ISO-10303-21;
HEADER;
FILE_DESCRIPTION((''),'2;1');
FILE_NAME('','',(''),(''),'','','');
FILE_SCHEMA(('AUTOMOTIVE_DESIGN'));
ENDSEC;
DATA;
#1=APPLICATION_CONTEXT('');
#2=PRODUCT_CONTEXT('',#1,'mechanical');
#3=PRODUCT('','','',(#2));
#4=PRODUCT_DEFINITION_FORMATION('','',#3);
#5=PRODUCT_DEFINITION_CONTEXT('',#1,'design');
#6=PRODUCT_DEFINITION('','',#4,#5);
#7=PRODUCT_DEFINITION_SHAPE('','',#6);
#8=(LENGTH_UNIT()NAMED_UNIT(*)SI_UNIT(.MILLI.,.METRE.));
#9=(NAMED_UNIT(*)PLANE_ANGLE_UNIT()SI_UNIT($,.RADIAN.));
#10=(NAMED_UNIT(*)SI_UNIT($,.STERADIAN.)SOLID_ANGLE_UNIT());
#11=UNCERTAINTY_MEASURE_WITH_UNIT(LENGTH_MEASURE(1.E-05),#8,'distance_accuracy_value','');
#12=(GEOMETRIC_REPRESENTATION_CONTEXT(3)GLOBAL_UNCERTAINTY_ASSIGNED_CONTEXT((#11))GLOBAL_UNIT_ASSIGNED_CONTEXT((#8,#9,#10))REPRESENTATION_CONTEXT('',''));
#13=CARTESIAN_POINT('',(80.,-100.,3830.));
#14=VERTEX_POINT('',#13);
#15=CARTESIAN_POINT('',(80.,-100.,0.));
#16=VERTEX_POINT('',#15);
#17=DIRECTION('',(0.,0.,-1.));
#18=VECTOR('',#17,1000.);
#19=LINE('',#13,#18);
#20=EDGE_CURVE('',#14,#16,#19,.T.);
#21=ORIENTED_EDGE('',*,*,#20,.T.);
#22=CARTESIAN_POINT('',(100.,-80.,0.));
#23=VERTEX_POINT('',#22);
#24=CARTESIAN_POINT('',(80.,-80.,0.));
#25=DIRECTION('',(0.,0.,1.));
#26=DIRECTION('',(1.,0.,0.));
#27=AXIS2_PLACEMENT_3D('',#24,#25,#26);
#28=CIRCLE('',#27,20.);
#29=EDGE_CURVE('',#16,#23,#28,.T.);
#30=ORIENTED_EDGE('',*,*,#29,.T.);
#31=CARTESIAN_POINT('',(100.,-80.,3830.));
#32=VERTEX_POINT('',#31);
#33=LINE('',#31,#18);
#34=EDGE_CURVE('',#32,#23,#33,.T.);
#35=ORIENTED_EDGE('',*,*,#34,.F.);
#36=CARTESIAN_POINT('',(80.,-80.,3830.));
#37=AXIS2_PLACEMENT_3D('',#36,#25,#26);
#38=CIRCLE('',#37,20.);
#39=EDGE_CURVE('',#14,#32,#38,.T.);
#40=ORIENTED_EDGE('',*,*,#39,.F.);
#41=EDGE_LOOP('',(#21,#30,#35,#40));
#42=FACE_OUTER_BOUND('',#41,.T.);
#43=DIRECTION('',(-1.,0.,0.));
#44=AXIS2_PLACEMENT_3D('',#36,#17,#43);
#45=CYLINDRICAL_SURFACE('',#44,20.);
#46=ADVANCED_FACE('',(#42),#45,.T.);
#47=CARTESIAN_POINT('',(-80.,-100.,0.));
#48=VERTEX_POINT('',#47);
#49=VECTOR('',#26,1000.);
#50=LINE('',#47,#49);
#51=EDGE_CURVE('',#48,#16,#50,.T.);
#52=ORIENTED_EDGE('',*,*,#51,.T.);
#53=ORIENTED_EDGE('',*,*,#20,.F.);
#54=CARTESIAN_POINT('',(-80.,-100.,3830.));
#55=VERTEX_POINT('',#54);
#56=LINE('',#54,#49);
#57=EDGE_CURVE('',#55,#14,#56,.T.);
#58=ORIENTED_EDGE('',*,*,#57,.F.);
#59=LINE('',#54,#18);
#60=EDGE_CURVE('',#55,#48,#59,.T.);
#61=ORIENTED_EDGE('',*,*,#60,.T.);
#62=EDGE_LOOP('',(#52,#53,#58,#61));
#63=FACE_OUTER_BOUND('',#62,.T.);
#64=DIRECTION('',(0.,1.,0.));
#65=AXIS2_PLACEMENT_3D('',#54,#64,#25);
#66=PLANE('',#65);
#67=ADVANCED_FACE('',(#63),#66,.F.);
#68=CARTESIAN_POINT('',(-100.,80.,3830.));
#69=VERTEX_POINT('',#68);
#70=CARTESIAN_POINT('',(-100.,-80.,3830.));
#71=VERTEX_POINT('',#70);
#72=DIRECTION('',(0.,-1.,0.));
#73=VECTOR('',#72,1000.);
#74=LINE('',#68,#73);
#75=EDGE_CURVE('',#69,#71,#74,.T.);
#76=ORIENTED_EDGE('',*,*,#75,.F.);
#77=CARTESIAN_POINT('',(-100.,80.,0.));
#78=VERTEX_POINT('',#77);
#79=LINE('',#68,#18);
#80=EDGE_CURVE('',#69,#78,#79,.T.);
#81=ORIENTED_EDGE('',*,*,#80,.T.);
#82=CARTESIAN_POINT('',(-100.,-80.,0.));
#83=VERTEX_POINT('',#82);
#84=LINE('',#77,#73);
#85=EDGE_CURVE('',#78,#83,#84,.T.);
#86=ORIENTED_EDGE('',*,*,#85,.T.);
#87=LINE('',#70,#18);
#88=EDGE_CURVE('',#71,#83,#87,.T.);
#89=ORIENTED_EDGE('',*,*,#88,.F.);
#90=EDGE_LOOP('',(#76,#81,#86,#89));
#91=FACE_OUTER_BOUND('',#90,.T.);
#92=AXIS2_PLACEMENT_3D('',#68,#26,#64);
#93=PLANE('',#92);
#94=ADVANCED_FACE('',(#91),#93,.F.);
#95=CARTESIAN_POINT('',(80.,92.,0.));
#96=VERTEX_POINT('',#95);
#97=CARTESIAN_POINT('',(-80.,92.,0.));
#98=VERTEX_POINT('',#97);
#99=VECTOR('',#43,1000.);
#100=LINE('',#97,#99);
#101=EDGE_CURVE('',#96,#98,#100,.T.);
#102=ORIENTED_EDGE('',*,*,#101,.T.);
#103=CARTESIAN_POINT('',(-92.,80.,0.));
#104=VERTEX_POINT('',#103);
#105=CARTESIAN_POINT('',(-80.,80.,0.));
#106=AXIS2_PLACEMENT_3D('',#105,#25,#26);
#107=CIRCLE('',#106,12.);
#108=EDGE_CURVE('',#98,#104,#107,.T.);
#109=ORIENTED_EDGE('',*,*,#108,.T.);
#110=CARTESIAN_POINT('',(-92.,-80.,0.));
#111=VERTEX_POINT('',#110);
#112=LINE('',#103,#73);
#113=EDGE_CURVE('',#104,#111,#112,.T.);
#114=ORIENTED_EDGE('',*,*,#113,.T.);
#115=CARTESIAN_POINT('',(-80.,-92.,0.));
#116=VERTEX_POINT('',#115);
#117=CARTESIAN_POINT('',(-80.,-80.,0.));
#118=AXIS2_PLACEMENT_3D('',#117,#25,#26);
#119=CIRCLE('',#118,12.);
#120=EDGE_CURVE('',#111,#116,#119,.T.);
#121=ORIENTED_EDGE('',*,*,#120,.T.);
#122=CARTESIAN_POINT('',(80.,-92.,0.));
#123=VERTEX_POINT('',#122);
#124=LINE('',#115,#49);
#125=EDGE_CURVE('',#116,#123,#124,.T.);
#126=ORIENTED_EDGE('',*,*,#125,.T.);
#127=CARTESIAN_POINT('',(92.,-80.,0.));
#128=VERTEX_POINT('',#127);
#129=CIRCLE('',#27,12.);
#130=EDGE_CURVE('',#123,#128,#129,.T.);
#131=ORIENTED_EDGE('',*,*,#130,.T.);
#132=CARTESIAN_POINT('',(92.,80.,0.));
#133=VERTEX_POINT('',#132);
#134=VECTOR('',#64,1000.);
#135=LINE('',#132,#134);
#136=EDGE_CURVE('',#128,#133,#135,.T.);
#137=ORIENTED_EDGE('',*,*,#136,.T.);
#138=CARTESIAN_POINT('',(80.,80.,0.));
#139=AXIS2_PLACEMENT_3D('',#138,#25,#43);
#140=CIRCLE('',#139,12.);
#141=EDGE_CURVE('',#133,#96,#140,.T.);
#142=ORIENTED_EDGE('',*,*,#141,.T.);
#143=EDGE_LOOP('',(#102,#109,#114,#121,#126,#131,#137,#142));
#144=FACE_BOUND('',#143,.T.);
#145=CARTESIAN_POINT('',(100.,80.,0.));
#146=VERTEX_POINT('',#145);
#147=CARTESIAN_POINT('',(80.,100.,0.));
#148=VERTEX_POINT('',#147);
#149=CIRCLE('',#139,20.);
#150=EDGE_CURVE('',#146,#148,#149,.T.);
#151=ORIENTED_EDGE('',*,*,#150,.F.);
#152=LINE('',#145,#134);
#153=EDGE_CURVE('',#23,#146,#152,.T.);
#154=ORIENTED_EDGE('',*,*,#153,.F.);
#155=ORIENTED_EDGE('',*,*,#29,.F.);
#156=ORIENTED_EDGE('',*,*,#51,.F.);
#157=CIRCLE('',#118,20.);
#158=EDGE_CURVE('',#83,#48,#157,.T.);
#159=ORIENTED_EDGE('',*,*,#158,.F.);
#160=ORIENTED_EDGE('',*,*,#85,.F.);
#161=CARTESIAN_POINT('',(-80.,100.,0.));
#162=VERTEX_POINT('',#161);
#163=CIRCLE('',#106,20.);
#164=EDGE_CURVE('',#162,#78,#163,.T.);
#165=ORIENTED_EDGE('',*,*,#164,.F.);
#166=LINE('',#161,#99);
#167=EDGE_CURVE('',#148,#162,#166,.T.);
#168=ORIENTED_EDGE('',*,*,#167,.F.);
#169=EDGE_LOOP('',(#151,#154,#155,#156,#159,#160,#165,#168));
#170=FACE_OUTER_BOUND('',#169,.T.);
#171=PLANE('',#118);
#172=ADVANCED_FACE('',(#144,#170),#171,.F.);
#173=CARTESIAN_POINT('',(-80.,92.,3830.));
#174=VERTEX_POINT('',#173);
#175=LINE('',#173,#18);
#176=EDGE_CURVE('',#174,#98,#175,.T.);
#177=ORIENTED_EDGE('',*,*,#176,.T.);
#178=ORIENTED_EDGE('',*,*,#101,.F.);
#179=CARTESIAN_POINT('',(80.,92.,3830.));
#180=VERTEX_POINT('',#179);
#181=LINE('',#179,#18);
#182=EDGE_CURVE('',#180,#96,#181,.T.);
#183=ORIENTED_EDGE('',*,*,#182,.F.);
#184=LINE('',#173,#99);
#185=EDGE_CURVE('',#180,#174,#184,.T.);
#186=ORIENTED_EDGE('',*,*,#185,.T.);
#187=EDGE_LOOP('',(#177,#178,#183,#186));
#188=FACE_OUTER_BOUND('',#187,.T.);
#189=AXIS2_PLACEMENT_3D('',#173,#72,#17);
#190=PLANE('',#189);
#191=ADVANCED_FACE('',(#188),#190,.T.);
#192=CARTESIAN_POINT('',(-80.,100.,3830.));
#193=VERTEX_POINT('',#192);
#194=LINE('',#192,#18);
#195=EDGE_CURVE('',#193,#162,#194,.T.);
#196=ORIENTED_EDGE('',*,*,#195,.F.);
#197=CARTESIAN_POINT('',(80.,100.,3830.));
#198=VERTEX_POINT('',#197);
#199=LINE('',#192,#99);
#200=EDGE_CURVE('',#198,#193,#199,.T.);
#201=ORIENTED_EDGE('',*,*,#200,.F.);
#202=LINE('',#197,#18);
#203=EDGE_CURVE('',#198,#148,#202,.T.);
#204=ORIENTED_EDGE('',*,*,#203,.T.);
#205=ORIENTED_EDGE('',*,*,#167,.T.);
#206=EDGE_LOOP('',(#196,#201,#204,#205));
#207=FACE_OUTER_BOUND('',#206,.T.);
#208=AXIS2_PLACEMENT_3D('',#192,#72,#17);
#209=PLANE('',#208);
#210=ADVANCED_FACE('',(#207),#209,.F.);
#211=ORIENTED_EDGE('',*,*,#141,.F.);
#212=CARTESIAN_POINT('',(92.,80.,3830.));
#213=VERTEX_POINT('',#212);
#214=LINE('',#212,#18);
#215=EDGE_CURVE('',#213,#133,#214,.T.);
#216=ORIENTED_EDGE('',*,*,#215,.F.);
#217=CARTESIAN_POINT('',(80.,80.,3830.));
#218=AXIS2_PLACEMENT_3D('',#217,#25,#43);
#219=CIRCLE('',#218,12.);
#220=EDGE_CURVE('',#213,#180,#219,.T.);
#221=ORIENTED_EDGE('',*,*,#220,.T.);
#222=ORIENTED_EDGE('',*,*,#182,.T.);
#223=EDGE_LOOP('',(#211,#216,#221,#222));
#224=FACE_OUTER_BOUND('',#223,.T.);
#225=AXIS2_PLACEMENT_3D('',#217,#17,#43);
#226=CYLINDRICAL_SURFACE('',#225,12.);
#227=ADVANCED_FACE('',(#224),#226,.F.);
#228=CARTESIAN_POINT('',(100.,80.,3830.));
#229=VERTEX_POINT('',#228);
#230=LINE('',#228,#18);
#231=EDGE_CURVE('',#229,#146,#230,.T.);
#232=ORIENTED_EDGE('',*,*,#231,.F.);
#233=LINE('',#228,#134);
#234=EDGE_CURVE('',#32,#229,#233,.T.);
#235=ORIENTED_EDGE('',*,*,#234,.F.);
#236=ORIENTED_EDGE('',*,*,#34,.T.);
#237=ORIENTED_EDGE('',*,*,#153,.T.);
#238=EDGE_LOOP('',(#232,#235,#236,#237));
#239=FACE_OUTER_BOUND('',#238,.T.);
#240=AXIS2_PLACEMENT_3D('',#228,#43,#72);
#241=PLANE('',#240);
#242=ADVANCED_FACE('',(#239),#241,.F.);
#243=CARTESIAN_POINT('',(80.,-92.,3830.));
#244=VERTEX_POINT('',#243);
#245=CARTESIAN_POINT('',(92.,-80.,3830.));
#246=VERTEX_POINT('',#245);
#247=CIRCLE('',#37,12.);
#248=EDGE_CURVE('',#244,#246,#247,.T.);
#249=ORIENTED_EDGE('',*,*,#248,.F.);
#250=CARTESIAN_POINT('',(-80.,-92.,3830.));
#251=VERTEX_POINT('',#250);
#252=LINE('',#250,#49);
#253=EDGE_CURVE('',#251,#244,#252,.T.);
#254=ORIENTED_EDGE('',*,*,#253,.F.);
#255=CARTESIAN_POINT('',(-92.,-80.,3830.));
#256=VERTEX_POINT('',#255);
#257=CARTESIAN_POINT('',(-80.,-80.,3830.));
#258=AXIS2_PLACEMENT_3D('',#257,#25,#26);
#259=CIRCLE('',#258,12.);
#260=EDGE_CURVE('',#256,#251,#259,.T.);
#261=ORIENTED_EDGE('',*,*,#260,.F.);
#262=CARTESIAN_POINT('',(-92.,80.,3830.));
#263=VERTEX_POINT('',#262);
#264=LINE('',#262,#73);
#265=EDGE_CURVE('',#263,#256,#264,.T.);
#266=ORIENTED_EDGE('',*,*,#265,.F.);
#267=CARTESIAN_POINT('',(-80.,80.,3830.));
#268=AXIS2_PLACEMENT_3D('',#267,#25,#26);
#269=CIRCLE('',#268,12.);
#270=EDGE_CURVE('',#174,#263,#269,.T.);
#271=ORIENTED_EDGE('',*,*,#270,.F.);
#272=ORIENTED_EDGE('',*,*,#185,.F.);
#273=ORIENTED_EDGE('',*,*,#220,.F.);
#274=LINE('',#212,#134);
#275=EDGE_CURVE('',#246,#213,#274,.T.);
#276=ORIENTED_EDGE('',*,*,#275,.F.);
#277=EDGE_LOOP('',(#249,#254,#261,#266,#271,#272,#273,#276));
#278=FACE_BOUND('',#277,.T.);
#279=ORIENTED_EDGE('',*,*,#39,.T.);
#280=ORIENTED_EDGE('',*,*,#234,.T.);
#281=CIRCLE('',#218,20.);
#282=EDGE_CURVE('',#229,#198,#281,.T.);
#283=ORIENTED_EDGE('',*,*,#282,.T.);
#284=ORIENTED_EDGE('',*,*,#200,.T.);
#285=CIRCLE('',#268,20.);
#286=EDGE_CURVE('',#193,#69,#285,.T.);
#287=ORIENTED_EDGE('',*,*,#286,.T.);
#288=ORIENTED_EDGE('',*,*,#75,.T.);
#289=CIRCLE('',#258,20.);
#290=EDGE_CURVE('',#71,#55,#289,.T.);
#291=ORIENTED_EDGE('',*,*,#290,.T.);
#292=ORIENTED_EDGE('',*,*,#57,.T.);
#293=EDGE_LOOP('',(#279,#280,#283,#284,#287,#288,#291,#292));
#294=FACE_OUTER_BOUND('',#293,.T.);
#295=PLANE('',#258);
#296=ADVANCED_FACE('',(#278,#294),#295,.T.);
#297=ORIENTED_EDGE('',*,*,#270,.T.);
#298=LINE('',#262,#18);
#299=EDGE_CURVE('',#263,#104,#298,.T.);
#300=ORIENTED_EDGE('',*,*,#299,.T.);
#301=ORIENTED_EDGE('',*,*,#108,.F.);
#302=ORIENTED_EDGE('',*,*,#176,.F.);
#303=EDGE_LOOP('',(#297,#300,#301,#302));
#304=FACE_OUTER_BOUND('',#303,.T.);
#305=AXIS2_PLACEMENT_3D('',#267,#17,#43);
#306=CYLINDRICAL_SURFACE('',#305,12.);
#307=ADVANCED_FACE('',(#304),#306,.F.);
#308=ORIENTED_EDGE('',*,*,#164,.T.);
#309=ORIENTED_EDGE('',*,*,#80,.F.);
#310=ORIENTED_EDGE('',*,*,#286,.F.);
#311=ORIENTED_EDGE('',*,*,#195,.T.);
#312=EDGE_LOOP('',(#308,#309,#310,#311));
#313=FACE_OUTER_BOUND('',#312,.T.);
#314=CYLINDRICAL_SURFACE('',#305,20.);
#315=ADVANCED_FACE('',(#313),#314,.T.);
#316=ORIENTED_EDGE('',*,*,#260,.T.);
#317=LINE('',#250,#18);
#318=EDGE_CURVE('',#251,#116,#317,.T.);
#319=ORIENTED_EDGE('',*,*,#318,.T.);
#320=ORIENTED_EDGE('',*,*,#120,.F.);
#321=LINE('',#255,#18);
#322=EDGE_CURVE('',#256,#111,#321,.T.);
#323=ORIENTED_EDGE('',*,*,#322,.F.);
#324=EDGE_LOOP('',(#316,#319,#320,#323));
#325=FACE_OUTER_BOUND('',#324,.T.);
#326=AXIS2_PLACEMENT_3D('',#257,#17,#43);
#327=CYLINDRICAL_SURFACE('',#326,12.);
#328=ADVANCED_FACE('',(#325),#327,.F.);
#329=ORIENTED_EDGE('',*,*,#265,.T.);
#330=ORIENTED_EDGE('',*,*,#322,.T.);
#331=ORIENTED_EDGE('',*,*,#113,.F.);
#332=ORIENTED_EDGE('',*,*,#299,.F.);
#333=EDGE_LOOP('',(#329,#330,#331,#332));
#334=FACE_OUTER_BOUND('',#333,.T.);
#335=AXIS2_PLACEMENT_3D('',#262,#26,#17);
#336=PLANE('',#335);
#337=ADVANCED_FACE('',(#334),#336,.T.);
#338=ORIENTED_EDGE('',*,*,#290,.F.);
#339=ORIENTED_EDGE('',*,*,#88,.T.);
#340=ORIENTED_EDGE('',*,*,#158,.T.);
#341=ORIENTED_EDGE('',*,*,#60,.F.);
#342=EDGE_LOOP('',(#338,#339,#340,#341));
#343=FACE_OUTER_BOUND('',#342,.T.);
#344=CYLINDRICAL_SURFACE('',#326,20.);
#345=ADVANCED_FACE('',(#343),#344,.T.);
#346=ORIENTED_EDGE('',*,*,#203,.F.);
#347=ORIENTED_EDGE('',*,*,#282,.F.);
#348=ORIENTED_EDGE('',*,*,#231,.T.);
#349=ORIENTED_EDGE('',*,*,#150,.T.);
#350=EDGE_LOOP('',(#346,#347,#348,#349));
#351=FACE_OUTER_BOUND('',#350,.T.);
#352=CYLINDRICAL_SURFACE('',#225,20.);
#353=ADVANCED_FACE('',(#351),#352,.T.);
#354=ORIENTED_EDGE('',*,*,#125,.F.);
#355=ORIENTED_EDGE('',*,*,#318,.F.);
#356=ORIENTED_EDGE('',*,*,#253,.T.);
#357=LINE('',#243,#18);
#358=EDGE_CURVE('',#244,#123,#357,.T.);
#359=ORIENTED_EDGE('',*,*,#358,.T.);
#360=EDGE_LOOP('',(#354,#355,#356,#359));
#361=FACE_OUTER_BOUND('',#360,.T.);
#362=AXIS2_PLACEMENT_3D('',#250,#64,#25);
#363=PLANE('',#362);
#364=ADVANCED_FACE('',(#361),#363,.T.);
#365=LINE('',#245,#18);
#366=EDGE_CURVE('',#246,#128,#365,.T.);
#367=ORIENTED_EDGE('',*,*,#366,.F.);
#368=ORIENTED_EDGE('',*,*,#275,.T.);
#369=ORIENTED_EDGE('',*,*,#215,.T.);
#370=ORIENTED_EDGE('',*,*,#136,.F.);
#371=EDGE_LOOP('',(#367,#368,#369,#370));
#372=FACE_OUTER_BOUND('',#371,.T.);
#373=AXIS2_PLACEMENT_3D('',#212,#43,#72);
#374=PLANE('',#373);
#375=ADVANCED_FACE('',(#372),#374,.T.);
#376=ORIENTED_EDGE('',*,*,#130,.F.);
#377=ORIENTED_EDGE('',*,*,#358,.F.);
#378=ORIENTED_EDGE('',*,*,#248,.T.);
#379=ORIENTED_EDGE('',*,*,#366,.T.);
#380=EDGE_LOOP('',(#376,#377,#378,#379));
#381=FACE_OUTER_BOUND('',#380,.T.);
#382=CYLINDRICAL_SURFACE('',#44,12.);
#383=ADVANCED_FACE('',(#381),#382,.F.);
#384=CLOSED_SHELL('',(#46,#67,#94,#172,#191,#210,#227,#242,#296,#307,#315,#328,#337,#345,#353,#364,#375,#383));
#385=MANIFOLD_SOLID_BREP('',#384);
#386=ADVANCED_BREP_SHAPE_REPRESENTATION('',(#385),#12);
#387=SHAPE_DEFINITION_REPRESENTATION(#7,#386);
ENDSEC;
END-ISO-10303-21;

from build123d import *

# Parameters (mm, degrees)
BOSS_EXTRUDE1_DEPTH = 3830


with BuildPart() as part:
    # Sketch1 → Boss-Extrude1 (new body)
    with BuildSketch(Plane.XY):
        with BuildLine():
            Line((-80, 100), (80, 100))
            ThreePointArc((80, 100), (94.142135624, 94.142135624), (100, 80))
            Line((100, 80), (100, -80))
            ThreePointArc((100, -80), (94.142135624, -94.142135624), (80, -100))
            Line((80, -100), (-80, -100))
            ThreePointArc((-80, -100), (-94.142135624, -94.142135624), (-100, -80))
            Line((-100, -80), (-100, 80))
            ThreePointArc((-100, 80), (-94.142135624, 94.142135624), (-80, 100))
        make_face()
        with BuildLine():
            Line((-92, 80), (-92, -80))
            ThreePointArc((-92, -80), (-88.485281374, -88.485281374), (-80, -92))
            Line((-80, -92), (80, -92))
            ThreePointArc((80, -92), (88.485281374, -88.485281374), (92, -80))
            Line((92, -80), (92, 80))
            ThreePointArc((92, 80), (88.485281374, 88.485281374), (80, 92))
            Line((80, 92), (-80, 92))
            ThreePointArc((-80, 92), (-88.485281374, 88.485281374), (-92, 80))
        make_face(mode=Mode.SUBTRACT)
    extrude(amount=BOSS_EXTRUDE1_DEPTH)


solid = part.part
